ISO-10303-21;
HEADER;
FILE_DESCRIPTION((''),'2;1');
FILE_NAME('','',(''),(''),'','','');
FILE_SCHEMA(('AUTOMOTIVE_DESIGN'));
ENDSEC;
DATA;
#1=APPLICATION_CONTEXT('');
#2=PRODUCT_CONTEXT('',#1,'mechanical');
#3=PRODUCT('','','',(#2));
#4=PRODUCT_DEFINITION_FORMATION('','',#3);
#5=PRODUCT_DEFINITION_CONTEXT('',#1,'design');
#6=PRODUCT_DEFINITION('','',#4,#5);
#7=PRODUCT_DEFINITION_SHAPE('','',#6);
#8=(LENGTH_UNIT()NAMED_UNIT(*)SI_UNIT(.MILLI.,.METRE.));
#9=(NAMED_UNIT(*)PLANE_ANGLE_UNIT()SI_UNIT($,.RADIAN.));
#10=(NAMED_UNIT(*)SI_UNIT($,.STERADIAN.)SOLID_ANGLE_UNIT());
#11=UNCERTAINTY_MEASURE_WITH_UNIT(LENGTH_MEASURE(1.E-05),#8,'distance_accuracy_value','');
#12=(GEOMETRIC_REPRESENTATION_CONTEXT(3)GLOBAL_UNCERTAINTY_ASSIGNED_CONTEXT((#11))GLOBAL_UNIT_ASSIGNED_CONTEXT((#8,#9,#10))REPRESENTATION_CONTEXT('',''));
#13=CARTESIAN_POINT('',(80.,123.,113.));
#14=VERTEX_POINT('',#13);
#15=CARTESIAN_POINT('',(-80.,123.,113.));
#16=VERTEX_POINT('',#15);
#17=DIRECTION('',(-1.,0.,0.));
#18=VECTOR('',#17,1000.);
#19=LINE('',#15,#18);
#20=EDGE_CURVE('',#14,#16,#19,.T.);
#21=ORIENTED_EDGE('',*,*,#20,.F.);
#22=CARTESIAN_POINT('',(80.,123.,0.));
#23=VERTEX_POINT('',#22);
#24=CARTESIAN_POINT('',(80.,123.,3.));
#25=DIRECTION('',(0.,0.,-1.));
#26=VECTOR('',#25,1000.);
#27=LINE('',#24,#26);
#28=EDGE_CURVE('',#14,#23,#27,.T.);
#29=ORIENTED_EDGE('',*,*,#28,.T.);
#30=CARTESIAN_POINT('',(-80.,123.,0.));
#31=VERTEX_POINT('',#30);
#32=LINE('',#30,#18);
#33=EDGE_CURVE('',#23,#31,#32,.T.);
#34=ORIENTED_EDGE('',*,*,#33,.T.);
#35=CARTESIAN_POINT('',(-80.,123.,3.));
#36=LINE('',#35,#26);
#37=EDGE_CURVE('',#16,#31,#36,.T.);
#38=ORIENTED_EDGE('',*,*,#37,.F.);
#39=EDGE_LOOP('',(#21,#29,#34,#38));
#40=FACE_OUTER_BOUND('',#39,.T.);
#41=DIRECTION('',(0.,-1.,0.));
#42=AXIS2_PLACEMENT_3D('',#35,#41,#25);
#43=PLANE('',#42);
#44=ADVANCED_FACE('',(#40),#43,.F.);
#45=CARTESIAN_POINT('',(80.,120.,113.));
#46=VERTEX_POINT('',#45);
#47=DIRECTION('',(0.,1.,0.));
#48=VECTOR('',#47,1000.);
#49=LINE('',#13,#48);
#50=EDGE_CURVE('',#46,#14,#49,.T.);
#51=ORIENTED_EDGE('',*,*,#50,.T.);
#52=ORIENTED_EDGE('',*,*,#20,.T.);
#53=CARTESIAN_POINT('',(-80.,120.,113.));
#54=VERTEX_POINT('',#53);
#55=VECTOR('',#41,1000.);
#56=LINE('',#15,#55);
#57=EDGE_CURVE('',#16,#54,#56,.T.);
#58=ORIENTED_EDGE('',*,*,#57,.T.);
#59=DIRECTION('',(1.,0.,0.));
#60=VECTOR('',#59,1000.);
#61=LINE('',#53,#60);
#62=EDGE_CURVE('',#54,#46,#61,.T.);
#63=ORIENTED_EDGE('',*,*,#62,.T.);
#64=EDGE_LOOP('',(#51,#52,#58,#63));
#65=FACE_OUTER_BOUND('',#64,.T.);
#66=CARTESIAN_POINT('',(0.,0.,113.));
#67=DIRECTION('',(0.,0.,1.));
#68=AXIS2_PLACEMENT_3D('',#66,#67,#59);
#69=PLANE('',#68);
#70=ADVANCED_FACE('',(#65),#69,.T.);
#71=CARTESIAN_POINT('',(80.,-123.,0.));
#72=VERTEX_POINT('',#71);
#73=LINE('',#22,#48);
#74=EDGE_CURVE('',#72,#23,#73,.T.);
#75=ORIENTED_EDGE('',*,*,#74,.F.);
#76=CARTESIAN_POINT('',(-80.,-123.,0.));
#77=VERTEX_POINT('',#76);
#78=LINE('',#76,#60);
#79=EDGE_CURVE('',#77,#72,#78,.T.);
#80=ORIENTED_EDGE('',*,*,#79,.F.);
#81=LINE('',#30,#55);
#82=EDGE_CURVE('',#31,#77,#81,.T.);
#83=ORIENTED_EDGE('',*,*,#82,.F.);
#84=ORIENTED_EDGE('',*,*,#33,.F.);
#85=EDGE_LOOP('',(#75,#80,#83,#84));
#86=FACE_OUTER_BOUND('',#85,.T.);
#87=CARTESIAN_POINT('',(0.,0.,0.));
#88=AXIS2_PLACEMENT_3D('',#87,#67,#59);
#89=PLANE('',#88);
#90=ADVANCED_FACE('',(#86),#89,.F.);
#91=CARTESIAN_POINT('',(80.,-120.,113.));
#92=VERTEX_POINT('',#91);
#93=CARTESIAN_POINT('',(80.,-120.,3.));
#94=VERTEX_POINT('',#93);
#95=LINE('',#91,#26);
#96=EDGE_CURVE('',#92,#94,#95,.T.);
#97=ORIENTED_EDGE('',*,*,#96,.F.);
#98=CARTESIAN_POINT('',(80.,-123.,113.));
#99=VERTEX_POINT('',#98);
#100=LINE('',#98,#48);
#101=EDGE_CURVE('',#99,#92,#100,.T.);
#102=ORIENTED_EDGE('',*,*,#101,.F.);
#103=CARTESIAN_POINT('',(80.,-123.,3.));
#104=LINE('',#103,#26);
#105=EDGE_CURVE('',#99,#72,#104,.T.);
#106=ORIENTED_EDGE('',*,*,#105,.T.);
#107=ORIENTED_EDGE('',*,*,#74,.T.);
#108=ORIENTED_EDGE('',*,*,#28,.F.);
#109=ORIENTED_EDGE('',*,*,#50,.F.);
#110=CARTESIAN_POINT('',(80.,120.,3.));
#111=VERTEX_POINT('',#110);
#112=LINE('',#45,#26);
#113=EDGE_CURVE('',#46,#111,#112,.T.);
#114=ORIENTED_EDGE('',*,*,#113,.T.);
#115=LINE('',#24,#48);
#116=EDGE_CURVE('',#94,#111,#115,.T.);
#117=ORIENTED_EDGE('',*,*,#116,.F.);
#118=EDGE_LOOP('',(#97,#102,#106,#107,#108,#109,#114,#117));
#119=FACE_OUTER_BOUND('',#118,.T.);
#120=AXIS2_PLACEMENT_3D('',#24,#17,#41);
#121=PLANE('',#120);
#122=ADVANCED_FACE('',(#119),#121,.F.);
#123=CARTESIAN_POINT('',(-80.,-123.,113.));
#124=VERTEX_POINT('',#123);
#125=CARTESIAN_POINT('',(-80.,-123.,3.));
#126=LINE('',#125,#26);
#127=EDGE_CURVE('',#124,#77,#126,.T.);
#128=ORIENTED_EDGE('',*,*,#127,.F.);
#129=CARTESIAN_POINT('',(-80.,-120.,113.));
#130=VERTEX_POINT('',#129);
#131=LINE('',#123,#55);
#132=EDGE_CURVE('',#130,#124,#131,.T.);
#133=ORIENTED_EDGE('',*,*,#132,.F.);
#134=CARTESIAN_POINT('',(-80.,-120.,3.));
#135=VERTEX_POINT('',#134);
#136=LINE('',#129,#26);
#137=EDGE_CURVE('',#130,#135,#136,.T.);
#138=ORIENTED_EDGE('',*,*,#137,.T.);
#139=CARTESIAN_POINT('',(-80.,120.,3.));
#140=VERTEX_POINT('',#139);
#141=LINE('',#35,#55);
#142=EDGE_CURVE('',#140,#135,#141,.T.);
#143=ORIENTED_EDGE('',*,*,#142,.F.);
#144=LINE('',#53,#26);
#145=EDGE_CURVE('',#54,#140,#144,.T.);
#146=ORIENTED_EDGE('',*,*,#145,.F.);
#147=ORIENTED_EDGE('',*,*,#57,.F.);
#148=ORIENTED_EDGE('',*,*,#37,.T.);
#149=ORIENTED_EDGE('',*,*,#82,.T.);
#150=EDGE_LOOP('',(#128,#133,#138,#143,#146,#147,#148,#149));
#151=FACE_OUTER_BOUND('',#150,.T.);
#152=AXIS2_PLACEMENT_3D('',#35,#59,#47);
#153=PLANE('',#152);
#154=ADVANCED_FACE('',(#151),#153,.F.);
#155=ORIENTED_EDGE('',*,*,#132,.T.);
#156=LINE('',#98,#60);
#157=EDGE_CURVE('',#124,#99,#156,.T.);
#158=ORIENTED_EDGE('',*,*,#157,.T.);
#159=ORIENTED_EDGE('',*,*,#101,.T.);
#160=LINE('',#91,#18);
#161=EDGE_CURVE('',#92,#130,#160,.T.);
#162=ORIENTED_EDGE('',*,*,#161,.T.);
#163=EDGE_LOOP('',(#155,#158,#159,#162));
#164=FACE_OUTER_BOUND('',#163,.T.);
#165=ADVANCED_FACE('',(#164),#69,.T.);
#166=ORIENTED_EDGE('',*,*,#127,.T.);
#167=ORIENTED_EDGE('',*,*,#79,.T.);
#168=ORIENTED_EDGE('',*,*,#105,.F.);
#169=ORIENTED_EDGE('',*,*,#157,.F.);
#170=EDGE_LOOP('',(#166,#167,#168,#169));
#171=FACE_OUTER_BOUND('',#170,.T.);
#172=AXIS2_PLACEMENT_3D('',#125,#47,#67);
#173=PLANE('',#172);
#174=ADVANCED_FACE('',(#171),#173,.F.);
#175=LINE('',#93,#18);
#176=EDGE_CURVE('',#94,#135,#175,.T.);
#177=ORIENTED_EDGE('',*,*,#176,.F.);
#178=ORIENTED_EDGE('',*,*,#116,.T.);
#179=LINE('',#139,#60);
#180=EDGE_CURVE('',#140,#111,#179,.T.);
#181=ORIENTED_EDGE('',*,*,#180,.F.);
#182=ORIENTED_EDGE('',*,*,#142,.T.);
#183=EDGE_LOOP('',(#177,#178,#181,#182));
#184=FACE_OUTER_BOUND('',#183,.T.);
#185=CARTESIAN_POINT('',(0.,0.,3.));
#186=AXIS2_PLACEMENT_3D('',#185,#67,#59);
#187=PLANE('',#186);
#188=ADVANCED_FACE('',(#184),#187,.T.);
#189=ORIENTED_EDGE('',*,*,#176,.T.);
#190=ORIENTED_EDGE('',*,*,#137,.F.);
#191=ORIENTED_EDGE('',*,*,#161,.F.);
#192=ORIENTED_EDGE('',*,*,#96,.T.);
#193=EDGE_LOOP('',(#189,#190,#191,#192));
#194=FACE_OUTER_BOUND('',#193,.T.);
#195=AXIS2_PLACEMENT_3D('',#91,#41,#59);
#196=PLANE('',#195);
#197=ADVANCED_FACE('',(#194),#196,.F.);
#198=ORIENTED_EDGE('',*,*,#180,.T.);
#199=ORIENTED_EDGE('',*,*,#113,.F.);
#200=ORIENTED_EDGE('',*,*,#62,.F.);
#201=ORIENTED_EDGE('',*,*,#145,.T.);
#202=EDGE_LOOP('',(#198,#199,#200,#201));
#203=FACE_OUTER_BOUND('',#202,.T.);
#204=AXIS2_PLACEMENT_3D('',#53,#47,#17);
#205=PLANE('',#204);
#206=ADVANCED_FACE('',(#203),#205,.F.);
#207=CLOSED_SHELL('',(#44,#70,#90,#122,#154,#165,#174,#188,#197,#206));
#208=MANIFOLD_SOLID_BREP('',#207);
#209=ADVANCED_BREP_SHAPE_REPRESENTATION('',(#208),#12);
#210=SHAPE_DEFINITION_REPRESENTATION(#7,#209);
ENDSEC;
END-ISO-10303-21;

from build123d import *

# Parameters (mm, degrees)
SKETCH1_W           = 160
SKETCH1_H           = 246
BOSS_EXTRUDE1_DEPTH = 3
SKETCH2_W           = 160
SKETCH2_H           = 3
BOSS_EXTRUDE2_DEPTH = 110


with BuildPart() as part:
    # Sketch1 → Boss-Extrude1 (new body)
    with BuildSketch(Plane.XY):
        Rectangle(SKETCH1_W, SKETCH1_H)
    extrude(amount=BOSS_EXTRUDE1_DEPTH)

    # Sketch2 → Boss-Extrude2 (add)
    with BuildSketch(Plane.XY.offset(3)):
        with Locations((0, 121.5)):
            Rectangle(SKETCH2_W, SKETCH2_H)
        with Locations((0, -121.5)):
            Rectangle(SKETCH2_W, SKETCH2_H)
    extrude(amount=BOSS_EXTRUDE2_DEPTH)


solid = part.part
